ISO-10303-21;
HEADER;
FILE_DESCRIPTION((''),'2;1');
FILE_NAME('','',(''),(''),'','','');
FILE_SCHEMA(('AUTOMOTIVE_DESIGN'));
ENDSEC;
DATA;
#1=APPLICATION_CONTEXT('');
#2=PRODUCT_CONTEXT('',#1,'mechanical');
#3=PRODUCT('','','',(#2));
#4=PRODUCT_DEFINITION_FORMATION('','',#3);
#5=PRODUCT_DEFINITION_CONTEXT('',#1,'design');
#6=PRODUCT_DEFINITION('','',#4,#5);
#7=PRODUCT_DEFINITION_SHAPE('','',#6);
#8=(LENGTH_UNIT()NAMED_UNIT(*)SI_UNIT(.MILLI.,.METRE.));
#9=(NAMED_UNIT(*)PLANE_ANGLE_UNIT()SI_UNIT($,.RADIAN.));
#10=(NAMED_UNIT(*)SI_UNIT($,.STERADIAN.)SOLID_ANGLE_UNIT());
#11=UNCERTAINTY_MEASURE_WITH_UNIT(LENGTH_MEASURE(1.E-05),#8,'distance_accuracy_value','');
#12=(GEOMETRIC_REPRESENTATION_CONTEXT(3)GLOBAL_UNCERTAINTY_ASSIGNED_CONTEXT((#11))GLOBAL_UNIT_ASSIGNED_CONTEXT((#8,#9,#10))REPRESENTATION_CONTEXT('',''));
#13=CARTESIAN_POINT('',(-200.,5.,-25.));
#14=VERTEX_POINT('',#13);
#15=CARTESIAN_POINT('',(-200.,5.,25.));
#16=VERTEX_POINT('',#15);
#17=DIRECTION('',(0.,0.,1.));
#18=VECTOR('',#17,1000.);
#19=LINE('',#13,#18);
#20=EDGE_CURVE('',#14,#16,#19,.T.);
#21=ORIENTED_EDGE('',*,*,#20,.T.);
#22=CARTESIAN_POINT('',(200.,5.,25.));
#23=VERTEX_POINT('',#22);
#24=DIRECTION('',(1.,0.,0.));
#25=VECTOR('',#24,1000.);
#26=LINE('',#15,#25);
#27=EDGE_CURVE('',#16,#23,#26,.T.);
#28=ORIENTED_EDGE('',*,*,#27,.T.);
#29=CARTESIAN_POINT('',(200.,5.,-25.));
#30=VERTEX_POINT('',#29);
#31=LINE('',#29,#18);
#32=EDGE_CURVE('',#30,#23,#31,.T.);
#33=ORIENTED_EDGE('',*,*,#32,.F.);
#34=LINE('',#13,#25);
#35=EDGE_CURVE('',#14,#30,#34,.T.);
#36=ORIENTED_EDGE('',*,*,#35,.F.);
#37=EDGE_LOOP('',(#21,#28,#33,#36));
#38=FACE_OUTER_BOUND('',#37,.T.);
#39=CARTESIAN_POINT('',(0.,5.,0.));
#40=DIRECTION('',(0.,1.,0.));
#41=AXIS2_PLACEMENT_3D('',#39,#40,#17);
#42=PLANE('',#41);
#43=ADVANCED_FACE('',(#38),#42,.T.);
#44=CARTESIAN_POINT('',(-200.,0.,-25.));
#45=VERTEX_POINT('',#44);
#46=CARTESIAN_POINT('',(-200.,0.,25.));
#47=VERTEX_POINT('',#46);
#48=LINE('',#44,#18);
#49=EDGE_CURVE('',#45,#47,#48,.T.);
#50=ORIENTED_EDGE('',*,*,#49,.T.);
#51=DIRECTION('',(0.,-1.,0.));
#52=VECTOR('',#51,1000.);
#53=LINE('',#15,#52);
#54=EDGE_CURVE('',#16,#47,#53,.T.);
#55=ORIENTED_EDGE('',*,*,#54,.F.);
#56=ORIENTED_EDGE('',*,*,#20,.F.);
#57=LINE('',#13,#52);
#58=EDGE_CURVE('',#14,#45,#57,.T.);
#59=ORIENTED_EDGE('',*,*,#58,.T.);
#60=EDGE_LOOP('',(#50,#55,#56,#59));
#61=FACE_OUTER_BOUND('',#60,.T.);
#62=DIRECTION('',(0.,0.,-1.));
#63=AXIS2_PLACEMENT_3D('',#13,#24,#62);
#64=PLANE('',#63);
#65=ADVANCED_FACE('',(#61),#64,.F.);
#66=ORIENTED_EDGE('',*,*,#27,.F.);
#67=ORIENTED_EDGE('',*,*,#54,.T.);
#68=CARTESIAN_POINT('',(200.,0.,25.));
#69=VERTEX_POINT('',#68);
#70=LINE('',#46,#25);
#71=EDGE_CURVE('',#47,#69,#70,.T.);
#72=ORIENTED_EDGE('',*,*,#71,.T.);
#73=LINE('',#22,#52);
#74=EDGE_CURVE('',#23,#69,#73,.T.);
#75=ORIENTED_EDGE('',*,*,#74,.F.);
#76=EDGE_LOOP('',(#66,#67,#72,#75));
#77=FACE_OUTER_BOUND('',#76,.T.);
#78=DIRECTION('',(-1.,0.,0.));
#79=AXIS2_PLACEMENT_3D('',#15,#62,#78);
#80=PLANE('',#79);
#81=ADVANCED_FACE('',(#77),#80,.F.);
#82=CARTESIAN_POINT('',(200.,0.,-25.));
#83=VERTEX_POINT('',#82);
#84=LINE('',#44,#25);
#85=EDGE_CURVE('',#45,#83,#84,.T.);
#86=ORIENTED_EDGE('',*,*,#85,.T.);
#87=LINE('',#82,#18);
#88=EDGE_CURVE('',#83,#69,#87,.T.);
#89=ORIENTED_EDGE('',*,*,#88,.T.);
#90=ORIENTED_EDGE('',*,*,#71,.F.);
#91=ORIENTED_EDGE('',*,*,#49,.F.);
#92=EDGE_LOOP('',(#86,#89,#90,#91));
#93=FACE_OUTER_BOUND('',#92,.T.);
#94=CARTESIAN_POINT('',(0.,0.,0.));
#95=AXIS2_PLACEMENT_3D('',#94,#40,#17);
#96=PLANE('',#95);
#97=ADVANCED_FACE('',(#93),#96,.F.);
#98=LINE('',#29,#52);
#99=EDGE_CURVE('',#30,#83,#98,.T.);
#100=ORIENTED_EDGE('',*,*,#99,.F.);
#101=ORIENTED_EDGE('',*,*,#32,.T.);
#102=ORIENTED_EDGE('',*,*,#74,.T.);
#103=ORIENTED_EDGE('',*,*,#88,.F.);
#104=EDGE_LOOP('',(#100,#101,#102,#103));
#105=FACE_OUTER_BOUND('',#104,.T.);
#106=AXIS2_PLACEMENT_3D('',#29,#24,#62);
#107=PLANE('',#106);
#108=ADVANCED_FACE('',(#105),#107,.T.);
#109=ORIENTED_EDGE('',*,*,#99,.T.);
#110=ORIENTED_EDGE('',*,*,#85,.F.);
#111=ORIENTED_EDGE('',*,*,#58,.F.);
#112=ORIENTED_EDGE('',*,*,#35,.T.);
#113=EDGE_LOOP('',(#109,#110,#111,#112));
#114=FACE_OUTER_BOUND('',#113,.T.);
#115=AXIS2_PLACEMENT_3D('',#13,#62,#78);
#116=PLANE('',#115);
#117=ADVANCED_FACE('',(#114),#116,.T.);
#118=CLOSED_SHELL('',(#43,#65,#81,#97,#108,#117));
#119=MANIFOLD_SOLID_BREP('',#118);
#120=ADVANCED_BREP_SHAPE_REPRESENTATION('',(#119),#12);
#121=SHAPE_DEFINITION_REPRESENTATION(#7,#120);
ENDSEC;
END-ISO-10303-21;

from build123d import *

# Parameters (mm, degrees)
SKETCH1_W           = 400
SKETCH1_H           = 50
BOSS_EXTRUDE1_DEPTH = 5


with BuildPart() as part:
    # Sketch1 → Boss-Extrude1 (new body)
    with BuildSketch(Plane(origin=(0, 0, 0), x_dir=(1, 0, 0), z_dir=(0, 1, 0))):
        Rectangle(SKETCH1_W, SKETCH1_H)
    extrude(amount=BOSS_EXTRUDE1_DEPTH)


solid = part.part
